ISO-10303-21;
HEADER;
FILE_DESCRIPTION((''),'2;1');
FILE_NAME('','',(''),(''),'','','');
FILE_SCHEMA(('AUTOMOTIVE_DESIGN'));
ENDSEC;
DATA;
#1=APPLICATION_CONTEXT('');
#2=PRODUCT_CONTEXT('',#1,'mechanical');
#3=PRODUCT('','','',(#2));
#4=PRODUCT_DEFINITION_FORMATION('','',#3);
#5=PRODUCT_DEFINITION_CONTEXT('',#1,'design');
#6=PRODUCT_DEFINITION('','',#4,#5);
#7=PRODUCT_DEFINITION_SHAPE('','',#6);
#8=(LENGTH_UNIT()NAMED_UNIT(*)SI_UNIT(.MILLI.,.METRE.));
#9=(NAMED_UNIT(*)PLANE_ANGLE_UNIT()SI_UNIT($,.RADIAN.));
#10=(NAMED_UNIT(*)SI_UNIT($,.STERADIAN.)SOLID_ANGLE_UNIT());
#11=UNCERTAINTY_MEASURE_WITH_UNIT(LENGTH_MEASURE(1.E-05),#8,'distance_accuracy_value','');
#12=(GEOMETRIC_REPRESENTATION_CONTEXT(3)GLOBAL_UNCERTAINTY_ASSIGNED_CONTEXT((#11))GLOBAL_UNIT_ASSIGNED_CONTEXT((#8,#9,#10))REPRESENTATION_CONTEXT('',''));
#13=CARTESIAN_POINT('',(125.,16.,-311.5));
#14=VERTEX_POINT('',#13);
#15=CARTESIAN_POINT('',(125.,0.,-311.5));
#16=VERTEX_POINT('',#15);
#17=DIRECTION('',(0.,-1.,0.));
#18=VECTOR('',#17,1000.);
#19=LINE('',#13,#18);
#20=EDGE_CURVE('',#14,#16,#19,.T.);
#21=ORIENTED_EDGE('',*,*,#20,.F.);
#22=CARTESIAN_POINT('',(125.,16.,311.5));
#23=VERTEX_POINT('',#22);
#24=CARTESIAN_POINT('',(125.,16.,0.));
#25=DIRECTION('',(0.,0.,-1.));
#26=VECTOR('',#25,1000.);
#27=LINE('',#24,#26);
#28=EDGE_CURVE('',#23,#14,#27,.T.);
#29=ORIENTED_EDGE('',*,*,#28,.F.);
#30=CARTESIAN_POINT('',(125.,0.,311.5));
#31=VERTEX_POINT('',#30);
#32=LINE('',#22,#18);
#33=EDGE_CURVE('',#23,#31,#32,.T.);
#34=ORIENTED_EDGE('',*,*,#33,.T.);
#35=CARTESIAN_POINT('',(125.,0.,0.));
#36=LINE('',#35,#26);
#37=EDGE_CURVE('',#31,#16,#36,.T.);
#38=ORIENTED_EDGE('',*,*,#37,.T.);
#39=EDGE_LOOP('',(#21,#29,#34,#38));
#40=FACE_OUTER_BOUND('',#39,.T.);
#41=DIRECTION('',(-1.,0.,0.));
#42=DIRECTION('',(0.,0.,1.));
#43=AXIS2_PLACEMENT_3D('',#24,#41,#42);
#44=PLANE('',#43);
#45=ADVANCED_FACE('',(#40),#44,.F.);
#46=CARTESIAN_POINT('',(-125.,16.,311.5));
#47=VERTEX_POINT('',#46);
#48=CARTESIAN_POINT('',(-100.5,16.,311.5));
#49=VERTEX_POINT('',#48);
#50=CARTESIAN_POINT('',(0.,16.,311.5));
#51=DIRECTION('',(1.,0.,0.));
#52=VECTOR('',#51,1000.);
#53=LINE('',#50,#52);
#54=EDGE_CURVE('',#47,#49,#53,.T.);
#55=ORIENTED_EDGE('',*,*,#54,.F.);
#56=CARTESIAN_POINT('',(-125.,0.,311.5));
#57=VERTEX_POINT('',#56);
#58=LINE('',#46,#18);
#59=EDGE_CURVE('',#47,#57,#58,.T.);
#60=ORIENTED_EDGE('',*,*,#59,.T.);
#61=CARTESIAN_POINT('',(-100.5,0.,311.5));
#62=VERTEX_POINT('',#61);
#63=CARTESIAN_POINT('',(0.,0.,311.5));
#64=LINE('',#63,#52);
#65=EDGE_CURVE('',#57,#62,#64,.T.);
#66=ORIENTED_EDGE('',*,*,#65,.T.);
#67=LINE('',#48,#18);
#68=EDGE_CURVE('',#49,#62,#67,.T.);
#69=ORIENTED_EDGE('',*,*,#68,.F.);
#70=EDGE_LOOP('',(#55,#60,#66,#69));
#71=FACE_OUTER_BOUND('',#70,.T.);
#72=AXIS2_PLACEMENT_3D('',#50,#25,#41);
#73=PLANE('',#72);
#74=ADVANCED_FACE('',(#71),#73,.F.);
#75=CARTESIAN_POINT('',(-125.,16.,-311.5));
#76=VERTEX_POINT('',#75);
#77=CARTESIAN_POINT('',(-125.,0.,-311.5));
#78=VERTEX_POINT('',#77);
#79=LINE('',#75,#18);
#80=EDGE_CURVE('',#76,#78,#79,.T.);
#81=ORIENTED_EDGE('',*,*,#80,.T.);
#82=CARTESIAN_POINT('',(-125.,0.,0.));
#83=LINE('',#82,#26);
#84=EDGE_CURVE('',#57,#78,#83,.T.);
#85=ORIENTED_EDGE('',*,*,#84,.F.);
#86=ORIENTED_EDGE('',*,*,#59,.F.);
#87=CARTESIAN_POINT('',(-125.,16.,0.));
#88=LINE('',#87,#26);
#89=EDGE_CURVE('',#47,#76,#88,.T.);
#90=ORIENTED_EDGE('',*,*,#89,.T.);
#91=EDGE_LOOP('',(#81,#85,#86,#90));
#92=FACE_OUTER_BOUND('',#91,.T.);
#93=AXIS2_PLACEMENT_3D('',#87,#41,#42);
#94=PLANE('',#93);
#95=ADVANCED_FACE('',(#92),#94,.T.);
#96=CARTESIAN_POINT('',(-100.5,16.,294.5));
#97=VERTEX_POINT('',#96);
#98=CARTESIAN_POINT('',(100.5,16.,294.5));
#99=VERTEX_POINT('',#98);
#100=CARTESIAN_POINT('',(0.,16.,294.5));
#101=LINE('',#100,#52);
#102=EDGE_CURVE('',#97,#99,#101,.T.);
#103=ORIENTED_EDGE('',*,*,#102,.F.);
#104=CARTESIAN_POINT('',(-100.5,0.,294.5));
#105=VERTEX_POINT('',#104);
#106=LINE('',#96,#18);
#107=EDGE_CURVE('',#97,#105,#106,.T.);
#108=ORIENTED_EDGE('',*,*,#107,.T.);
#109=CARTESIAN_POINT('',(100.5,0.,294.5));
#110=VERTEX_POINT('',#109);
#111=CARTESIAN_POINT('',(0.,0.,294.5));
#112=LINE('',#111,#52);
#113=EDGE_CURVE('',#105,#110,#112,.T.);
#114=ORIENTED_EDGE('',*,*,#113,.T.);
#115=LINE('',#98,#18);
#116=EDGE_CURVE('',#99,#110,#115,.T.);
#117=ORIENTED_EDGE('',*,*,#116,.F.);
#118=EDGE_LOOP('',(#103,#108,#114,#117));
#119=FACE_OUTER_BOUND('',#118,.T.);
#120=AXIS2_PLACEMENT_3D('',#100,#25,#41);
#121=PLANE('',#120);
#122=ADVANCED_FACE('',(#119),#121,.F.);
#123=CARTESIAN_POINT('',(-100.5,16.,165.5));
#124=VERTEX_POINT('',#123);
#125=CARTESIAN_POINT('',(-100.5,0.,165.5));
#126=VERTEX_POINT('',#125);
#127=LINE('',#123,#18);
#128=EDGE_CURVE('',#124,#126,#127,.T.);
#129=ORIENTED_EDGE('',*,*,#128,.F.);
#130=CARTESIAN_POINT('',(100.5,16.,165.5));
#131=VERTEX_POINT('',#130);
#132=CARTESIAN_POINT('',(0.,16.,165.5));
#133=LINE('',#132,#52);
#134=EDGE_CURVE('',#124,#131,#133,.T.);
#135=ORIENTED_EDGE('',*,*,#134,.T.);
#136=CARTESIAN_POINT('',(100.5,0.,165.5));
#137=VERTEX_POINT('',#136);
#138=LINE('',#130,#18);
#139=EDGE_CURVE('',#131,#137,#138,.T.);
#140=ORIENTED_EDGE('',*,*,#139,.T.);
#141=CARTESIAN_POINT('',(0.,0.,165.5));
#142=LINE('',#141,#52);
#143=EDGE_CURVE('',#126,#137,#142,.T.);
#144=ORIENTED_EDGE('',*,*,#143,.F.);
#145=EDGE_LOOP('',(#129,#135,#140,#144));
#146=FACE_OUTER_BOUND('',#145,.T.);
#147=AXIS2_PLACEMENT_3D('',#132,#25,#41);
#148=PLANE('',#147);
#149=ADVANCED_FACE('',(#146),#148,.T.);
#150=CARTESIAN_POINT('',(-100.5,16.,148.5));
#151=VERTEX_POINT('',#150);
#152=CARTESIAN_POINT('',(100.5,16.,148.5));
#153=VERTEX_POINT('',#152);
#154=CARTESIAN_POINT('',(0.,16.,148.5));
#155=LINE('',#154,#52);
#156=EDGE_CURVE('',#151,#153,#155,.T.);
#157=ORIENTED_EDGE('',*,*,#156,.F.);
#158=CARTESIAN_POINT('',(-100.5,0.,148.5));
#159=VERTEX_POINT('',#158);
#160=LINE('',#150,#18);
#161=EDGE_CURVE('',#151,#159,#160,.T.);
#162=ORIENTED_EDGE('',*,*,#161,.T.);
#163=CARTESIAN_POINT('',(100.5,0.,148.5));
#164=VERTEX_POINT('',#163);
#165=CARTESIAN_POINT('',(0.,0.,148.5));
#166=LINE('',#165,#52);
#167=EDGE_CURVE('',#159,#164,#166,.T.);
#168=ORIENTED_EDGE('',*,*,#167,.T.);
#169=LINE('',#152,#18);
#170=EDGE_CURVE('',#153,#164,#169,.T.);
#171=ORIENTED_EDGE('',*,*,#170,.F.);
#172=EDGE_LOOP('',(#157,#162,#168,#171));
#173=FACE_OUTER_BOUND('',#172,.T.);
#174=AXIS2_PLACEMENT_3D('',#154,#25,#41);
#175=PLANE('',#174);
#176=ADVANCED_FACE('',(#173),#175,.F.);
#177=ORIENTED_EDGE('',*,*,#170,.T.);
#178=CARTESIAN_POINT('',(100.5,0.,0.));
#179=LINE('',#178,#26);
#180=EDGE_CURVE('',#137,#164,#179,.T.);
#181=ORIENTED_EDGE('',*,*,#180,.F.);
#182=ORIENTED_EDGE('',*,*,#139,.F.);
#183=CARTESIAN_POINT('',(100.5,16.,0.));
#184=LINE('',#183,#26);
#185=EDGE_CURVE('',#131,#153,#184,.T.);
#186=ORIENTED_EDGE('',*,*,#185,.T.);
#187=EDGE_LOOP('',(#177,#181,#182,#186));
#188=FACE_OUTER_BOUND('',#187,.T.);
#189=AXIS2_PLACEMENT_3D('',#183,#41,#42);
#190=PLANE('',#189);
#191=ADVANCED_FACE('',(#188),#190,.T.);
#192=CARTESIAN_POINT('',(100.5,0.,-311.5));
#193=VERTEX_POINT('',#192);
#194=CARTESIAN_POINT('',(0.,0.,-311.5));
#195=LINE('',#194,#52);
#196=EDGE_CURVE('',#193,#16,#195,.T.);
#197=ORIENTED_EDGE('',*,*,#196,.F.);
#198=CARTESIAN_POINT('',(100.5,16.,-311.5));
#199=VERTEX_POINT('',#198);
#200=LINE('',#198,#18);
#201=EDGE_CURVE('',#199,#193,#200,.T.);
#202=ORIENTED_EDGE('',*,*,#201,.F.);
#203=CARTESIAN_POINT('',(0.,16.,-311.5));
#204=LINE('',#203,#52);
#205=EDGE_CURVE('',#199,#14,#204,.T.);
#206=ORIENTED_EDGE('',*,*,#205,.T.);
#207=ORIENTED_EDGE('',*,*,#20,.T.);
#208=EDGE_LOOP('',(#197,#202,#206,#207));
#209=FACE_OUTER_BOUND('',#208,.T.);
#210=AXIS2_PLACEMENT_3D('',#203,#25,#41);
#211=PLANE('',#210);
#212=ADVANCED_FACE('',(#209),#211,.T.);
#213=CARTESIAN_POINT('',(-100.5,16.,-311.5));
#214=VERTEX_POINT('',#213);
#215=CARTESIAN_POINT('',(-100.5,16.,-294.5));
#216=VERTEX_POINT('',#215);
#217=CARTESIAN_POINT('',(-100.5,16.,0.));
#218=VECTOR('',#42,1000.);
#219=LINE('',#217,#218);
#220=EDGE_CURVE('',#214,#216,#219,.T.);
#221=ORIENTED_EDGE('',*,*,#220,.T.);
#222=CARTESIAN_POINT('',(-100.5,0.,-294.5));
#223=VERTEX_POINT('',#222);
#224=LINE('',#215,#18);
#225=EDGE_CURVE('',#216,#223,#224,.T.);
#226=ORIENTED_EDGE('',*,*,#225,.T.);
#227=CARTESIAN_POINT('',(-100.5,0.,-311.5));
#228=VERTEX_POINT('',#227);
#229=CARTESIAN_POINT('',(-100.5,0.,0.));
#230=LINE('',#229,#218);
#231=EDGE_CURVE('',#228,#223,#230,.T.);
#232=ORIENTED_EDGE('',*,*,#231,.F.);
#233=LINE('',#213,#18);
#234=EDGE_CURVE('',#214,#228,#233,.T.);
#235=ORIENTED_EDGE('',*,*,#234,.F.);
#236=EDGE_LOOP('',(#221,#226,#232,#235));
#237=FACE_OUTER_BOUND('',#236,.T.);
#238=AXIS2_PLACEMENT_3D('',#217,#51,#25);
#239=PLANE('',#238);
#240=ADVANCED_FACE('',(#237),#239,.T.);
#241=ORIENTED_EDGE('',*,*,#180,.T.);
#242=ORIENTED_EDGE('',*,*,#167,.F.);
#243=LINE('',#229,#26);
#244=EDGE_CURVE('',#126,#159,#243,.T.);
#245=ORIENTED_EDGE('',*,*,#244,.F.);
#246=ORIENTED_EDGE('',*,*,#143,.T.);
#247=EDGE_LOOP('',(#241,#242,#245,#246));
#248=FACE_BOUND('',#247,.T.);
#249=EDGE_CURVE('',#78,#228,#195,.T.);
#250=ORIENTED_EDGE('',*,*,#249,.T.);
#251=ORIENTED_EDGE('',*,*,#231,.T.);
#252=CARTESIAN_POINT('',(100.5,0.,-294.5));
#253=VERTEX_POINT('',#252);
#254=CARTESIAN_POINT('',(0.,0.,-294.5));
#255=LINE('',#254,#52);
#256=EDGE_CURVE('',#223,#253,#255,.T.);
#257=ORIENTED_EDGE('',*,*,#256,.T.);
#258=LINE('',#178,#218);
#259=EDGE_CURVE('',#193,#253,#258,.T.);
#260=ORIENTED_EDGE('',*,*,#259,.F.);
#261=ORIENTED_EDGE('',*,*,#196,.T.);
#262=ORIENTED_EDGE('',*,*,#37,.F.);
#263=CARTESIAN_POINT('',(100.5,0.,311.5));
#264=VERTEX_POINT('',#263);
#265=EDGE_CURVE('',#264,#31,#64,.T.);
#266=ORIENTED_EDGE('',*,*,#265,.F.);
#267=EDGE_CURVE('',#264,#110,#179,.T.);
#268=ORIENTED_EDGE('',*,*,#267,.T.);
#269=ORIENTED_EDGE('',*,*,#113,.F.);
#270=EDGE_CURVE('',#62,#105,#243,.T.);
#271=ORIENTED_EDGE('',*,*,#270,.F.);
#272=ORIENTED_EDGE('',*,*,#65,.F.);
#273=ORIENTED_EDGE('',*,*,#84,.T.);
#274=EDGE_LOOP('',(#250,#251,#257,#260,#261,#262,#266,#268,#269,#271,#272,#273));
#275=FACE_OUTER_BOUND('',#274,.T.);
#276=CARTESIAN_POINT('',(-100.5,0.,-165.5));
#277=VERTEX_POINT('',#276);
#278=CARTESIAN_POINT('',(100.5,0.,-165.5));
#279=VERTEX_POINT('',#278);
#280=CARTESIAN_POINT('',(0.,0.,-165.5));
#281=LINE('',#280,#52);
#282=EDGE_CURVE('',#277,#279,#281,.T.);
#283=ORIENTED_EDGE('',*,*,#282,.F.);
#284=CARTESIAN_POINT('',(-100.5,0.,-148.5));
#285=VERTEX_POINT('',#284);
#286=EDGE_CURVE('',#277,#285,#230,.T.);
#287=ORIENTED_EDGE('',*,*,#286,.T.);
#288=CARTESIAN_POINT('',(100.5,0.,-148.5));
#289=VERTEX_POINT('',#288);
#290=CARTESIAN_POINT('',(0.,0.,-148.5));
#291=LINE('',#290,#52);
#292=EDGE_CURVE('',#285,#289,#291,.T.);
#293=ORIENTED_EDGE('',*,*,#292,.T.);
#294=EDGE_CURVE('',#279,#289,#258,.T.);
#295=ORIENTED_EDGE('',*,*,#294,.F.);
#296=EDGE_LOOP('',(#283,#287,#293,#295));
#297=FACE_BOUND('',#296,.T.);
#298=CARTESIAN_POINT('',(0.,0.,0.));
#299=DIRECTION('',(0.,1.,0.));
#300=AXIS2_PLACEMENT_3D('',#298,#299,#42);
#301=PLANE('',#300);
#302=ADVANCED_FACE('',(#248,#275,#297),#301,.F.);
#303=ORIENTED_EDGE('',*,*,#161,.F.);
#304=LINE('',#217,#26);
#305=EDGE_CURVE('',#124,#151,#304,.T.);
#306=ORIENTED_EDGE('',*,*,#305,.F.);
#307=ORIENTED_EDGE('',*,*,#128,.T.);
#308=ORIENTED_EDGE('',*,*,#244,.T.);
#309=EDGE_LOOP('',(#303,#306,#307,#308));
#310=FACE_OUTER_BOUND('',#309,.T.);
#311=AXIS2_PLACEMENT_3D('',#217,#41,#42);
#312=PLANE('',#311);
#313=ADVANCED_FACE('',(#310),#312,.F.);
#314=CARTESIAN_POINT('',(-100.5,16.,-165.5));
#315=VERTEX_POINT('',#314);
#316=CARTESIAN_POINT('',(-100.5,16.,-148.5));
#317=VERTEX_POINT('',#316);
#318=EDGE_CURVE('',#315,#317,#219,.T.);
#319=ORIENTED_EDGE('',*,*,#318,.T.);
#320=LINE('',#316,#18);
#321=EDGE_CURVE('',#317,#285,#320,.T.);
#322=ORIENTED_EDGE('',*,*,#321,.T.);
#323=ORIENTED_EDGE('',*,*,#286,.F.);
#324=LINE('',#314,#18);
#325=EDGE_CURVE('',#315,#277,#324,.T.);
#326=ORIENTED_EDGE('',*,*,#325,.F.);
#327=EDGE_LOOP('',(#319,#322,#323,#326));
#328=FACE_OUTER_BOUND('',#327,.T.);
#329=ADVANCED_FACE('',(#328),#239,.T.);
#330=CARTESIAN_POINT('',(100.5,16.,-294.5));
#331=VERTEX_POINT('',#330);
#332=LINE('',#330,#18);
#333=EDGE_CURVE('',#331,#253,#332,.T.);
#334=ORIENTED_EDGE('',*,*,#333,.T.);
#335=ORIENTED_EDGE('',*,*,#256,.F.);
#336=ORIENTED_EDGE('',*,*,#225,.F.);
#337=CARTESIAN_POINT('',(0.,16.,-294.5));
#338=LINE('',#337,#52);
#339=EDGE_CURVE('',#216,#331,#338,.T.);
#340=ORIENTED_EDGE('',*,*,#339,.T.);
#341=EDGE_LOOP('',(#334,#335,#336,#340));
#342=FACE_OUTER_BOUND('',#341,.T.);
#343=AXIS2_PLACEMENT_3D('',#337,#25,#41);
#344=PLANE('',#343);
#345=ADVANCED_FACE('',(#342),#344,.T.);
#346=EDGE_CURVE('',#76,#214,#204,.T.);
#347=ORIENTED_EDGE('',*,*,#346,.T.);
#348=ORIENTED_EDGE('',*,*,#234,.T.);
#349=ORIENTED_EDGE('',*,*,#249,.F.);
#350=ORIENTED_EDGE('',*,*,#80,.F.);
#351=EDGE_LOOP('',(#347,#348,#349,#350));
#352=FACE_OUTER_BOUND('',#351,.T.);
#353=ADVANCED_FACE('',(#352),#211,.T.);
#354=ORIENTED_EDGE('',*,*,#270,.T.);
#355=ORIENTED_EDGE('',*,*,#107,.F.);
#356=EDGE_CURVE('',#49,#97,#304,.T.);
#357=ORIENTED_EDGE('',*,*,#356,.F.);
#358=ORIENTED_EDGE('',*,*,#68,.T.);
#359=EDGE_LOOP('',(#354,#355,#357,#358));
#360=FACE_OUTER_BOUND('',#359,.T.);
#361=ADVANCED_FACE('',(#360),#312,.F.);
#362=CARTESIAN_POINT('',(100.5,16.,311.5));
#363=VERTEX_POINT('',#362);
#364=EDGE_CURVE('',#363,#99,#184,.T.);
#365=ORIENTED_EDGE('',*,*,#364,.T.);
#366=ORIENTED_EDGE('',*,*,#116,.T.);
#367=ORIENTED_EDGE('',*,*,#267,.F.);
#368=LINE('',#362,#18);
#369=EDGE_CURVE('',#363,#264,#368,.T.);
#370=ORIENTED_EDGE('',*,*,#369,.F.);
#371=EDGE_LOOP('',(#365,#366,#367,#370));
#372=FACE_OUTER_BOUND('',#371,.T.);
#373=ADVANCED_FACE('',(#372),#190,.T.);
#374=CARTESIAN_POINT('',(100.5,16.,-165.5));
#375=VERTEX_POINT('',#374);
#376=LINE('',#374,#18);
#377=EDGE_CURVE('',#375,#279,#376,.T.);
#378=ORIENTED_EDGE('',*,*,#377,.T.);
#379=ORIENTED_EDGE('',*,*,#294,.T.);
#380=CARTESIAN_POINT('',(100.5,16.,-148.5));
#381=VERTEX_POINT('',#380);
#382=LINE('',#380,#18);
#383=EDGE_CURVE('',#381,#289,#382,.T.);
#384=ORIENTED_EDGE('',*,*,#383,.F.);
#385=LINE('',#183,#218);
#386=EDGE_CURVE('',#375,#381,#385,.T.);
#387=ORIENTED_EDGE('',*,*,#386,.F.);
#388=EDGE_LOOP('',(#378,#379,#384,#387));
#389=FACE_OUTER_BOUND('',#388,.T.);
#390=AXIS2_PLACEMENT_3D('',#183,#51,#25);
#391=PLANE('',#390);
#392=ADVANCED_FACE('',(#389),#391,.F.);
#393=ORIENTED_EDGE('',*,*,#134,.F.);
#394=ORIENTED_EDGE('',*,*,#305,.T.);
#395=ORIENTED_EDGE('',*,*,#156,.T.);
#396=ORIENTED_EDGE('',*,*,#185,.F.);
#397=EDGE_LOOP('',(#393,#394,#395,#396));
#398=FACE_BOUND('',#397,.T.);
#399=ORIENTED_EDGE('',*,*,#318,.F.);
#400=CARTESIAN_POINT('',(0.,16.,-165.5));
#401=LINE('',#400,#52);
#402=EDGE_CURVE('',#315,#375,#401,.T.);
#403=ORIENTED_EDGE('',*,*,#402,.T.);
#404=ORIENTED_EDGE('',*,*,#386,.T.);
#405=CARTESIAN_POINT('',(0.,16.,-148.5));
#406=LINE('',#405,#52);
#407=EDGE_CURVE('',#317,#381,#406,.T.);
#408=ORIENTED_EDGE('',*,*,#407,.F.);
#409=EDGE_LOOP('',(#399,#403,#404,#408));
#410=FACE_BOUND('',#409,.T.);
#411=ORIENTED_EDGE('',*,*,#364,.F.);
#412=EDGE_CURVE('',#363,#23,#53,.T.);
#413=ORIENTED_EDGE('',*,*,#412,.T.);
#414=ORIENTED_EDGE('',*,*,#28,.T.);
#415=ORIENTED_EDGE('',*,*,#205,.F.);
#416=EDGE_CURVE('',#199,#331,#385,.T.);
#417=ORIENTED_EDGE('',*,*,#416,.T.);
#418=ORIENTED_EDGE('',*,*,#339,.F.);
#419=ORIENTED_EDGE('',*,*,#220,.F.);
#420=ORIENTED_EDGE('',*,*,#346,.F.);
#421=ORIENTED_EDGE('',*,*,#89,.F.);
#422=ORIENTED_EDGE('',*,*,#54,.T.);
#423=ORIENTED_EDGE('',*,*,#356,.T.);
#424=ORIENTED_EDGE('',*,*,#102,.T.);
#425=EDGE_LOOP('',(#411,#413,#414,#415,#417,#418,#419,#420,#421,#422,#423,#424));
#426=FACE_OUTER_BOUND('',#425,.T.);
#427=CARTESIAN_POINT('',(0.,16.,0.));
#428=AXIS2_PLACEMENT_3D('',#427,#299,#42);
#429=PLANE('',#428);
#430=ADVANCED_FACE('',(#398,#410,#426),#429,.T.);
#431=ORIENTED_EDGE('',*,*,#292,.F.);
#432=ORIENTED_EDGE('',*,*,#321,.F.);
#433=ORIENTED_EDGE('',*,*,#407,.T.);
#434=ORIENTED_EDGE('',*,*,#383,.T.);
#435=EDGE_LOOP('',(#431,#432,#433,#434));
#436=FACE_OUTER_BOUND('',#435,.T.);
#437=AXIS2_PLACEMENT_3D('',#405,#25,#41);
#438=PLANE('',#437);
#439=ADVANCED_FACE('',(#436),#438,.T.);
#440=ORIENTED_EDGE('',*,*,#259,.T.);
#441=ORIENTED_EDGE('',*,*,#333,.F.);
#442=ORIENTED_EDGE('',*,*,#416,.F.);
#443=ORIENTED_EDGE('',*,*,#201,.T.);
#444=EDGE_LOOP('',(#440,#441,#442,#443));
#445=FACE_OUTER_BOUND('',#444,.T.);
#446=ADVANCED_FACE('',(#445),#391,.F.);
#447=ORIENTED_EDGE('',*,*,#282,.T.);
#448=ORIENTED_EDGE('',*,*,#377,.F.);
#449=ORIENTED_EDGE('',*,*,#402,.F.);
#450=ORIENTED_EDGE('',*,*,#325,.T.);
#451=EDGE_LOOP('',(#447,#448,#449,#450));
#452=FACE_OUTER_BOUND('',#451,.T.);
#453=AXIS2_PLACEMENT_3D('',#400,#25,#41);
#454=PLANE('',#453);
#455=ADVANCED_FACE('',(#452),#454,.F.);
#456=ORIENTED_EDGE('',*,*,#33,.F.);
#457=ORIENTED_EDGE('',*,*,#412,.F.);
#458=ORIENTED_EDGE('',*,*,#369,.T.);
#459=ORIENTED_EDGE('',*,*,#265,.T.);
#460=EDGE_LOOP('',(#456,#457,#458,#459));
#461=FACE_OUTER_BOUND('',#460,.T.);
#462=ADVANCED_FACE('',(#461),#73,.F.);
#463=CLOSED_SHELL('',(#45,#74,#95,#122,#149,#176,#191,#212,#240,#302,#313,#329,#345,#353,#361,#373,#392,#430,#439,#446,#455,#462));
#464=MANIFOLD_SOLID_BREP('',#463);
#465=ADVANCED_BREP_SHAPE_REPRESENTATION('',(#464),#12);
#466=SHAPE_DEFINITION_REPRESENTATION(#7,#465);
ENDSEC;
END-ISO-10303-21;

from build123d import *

# Parameters (mm, degrees)
SKETCH1_W           = 201
SKETCH1_H           = 17
BOSS_EXTRUDE1_DEPTH = 16


with BuildPart() as part:
    # Sketch1 → Boss-Extrude1 (new body)
    with BuildSketch(Plane(origin=(0, 0, 0), x_dir=(1, 0, 0), z_dir=(0, 1, 0))):
        Polygon((-125, 311.5), (-125, -311.5), (-100.5, -311.5), (-100.5, -294.5), (100.5, -294.5), (100.5, -311.5), (125, -311.5), (125, 311.5), (100.5, 311.5), (100.5, 294.5), (-100.5, 294.5), (-100.5, 311.5), align=None)
        with Locations((0, -157)):
            Rectangle(SKETCH1_W, SKETCH1_H, mode=Mode.SUBTRACT)
        with Locations((0, 157)):
            Rectangle(SKETCH1_W, SKETCH1_H, mode=Mode.SUBTRACT)
    extrude(amount=BOSS_EXTRUDE1_DEPTH)


solid = part.part
